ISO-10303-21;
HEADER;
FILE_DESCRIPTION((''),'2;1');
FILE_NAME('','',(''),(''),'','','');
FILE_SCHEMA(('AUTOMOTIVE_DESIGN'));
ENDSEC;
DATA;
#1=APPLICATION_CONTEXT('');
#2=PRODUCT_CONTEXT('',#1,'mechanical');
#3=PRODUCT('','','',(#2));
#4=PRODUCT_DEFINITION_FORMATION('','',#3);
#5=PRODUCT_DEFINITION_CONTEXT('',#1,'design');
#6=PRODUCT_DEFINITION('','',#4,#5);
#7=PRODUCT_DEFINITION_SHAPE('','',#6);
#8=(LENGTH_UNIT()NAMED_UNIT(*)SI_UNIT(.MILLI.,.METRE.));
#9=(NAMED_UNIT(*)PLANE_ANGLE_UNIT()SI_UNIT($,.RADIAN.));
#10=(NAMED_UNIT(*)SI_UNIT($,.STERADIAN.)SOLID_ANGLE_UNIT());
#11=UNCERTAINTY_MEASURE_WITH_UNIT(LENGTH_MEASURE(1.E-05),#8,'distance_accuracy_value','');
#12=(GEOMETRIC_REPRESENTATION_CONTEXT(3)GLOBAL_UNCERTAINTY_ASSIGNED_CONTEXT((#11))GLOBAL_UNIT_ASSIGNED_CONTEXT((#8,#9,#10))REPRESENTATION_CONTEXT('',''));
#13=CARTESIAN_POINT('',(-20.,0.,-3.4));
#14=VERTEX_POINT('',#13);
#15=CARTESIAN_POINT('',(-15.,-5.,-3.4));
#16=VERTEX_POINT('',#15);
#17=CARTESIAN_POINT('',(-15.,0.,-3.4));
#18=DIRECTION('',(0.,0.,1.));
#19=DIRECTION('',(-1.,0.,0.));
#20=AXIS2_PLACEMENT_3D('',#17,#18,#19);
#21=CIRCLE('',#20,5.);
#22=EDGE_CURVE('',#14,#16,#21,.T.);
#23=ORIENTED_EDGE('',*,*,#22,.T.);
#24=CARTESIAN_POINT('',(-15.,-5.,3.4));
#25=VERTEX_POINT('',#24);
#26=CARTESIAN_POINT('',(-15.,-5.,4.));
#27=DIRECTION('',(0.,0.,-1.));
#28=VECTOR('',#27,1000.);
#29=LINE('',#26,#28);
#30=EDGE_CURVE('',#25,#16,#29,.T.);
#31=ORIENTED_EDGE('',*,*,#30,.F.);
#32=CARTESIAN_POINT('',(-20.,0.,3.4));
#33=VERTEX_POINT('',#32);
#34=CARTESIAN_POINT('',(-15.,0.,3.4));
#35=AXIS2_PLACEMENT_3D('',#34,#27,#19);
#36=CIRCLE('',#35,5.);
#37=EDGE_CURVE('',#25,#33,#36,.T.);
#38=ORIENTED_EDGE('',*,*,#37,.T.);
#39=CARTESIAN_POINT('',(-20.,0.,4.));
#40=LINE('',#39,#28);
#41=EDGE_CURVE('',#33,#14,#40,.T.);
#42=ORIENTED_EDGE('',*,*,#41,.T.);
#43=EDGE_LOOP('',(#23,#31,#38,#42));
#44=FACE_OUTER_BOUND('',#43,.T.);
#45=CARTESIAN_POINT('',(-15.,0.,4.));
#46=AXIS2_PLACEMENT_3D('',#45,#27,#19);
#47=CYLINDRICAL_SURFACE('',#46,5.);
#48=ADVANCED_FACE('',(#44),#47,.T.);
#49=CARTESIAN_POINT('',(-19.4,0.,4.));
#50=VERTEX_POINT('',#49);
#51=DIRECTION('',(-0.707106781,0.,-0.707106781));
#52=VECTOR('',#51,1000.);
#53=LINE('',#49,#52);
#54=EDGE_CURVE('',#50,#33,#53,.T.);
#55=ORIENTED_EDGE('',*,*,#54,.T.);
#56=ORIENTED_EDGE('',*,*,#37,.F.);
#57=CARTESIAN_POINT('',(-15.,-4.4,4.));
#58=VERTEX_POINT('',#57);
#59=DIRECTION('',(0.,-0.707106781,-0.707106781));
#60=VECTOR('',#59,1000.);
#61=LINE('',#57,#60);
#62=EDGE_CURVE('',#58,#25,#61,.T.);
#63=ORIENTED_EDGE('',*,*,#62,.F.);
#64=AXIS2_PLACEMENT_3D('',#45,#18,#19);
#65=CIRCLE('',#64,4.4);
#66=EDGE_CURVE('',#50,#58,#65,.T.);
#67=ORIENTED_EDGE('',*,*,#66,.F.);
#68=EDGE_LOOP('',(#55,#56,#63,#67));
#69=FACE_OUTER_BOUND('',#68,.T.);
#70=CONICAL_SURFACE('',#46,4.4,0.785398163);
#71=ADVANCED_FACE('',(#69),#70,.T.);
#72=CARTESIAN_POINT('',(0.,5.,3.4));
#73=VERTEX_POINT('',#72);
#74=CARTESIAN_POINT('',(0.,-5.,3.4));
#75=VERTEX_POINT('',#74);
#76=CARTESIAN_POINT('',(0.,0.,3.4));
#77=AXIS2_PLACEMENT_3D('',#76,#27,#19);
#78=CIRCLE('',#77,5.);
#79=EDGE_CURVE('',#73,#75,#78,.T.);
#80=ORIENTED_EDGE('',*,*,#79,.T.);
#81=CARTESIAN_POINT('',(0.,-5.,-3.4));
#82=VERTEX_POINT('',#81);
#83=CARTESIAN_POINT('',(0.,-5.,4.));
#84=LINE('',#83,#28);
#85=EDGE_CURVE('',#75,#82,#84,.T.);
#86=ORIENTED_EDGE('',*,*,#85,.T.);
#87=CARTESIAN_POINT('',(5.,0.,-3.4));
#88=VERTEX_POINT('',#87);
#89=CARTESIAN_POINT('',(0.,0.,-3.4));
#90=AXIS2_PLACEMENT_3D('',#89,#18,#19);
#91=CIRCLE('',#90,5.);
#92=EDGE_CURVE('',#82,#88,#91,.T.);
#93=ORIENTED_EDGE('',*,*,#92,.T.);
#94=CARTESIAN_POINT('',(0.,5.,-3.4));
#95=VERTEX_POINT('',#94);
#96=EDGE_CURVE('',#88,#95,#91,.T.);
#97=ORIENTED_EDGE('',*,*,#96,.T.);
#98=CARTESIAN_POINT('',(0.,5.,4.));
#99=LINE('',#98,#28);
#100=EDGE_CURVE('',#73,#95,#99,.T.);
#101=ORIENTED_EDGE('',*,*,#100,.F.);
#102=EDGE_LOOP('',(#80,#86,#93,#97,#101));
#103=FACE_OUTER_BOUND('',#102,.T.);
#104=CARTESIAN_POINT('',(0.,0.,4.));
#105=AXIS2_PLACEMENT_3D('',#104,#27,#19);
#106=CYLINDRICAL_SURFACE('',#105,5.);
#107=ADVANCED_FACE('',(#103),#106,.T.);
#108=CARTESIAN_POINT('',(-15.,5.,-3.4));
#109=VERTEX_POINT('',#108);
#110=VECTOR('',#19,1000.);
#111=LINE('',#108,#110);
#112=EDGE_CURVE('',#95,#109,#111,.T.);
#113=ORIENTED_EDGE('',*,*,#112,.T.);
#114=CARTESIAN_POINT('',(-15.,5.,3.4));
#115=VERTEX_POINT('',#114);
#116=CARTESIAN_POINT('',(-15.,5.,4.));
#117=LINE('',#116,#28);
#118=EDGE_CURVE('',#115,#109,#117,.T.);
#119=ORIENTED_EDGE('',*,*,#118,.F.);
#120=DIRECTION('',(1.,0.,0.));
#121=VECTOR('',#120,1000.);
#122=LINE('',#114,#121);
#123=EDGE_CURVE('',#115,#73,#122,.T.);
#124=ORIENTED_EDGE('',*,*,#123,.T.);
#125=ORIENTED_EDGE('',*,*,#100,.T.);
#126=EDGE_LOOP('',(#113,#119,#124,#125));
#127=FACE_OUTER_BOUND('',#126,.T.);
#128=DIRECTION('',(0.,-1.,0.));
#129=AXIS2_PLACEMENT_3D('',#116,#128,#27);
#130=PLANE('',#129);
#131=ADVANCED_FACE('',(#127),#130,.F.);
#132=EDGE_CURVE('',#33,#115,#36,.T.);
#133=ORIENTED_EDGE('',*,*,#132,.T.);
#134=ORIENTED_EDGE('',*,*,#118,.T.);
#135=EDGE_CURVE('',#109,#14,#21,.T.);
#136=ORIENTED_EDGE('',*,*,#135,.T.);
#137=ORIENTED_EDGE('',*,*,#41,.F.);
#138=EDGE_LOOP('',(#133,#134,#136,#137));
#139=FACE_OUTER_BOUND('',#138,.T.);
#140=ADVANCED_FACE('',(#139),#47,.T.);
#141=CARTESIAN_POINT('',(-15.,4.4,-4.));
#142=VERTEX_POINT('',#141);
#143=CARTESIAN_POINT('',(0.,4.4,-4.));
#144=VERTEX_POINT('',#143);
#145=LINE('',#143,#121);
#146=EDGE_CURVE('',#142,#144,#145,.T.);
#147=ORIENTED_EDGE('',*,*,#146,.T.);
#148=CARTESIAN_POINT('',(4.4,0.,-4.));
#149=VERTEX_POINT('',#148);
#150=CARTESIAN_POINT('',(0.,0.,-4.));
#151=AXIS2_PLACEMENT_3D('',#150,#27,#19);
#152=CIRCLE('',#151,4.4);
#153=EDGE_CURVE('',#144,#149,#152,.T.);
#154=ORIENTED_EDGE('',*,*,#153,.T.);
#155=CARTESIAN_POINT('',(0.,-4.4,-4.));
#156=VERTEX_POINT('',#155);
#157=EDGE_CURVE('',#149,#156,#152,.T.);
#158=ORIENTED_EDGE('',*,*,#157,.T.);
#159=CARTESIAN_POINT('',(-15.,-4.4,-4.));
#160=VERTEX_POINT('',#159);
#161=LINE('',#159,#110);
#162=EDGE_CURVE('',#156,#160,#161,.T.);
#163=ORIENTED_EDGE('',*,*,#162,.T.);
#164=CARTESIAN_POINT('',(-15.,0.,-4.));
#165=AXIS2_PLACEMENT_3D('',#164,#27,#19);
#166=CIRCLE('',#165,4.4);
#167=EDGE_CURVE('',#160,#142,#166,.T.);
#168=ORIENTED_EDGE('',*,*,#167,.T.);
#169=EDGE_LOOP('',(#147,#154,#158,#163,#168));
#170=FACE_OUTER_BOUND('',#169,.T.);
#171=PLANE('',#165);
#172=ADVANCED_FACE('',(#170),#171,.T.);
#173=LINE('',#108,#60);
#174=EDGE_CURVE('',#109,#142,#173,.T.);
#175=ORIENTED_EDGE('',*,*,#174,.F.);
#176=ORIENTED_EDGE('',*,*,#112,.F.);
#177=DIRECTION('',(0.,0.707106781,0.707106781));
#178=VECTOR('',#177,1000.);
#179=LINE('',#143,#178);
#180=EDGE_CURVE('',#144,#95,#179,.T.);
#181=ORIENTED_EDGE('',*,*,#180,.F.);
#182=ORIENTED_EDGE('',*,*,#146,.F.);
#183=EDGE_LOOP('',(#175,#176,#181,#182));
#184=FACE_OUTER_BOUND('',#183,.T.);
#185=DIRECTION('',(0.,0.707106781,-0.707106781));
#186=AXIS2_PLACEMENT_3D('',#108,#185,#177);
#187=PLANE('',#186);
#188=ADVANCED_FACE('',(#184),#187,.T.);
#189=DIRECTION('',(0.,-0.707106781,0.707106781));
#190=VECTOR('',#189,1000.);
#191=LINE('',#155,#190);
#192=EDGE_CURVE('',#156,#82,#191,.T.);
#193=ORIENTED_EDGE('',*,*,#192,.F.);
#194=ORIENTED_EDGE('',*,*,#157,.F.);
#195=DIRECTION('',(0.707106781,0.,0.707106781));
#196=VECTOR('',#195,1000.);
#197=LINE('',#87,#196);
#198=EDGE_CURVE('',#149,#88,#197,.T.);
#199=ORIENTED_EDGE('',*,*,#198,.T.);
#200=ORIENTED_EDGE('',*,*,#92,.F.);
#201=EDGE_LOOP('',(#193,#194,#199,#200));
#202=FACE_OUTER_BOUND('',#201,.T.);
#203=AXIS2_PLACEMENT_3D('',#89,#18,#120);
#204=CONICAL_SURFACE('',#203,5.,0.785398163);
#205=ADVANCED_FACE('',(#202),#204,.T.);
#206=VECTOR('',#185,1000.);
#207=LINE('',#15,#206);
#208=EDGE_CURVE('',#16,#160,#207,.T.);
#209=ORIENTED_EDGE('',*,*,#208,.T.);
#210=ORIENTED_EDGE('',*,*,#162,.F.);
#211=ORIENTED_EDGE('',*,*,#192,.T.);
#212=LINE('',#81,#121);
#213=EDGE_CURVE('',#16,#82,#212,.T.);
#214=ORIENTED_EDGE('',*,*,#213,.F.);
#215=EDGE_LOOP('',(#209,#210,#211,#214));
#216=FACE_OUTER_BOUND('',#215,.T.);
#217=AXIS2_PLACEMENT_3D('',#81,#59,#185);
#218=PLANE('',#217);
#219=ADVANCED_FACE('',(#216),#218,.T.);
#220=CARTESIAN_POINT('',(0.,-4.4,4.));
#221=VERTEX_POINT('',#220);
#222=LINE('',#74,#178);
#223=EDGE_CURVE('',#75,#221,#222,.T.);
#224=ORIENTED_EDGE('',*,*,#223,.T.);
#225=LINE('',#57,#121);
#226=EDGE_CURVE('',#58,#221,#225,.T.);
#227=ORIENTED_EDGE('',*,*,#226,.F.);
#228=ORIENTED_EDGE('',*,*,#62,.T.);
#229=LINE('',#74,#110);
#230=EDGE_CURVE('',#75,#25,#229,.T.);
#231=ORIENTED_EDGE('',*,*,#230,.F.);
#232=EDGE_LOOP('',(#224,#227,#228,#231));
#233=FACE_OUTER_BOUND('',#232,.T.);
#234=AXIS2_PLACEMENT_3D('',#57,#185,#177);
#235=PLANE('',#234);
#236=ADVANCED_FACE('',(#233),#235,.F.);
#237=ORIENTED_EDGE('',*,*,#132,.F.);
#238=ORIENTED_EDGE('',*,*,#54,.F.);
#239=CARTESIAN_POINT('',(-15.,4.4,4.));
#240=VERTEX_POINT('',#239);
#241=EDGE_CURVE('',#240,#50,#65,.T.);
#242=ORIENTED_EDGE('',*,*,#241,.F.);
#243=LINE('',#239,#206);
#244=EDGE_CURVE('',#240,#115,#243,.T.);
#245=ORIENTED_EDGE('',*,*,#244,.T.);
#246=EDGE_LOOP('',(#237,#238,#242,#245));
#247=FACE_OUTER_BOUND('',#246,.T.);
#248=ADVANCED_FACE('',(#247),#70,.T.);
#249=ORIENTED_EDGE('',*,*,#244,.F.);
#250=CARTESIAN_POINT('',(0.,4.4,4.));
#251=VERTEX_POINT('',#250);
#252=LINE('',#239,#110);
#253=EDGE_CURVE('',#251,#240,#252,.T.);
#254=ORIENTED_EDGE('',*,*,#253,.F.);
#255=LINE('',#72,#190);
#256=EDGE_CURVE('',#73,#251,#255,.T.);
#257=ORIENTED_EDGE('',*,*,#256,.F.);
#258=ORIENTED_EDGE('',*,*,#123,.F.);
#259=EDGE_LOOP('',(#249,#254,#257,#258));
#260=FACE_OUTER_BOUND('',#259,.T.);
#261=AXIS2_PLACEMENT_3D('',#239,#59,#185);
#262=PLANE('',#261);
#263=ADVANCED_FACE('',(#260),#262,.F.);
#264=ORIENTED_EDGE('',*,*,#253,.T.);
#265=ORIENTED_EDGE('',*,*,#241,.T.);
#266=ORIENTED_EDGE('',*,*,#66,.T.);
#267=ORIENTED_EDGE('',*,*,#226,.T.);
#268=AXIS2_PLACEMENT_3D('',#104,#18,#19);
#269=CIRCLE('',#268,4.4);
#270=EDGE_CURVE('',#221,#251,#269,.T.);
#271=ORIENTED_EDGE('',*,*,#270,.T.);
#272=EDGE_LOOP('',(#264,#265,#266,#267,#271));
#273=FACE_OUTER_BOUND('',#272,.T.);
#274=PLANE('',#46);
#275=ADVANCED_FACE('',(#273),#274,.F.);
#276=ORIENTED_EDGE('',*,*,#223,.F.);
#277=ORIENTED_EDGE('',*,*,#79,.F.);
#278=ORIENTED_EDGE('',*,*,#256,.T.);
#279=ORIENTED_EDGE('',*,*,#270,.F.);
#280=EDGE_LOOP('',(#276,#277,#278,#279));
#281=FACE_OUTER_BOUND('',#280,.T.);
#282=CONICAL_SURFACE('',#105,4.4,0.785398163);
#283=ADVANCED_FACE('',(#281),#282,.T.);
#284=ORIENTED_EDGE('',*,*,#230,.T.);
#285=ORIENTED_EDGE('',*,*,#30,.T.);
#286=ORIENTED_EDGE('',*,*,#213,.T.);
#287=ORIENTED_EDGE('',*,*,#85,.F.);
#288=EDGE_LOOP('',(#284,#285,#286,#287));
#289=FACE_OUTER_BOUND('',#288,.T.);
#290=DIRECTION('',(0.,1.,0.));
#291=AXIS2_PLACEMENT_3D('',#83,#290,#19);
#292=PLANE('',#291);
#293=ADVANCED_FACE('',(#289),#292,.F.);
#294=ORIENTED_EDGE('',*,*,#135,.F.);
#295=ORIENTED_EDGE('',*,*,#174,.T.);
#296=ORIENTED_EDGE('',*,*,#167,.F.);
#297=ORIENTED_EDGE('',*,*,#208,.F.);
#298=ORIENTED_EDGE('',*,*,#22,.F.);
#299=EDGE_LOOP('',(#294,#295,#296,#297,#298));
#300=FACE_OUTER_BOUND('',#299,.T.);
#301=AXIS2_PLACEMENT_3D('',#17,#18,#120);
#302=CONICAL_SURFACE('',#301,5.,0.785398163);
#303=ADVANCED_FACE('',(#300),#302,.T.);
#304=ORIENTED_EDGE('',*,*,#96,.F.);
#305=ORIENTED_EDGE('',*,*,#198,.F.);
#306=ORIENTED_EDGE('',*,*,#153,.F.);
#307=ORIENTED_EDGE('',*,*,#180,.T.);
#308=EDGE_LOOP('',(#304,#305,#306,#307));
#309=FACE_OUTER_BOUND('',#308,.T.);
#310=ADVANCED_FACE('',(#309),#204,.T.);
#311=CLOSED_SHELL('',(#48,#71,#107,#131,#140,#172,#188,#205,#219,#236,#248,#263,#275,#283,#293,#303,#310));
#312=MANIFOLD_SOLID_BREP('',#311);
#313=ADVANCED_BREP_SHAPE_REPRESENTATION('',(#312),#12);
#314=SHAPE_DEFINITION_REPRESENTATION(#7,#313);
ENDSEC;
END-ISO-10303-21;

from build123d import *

# Parameters (mm, degrees)
BASEKEY_DEPTH = 4
CHAMFER1_SIZE = 0.6


with BuildPart() as part:
    # Sketch1 → BaseKey (new, symmetric)
    with BuildSketch(Plane.XY):
        with BuildLine():
            Line((-15, 5), (0, 5))
            ThreePointArc((0, 5), (5, 0), (0, -5))
            Line((0, -5), (-15, -5))
            ThreePointArc((-15, -5), (-20, 0), (-15, 5))
        make_face()
    extrude(amount=BASEKEY_DEPTH, both=True)

    # Chamfer1
    chamfer1_edges = [part.edges().sort_by_distance(p)[0] for p in [
        (5, 0, 4),
        (-7.5, 5, 4),
        (-20, 0, 4),
        (-7.5, 5, -4),
        (5, 0, -4),
        (-7.5, -5, -4),
        (-20, 0, -4),
        (-7.5, -5, 4),
    ]]
    chamfer(chamfer1_edges, length=CHAMFER1_SIZE)


solid = part.part
